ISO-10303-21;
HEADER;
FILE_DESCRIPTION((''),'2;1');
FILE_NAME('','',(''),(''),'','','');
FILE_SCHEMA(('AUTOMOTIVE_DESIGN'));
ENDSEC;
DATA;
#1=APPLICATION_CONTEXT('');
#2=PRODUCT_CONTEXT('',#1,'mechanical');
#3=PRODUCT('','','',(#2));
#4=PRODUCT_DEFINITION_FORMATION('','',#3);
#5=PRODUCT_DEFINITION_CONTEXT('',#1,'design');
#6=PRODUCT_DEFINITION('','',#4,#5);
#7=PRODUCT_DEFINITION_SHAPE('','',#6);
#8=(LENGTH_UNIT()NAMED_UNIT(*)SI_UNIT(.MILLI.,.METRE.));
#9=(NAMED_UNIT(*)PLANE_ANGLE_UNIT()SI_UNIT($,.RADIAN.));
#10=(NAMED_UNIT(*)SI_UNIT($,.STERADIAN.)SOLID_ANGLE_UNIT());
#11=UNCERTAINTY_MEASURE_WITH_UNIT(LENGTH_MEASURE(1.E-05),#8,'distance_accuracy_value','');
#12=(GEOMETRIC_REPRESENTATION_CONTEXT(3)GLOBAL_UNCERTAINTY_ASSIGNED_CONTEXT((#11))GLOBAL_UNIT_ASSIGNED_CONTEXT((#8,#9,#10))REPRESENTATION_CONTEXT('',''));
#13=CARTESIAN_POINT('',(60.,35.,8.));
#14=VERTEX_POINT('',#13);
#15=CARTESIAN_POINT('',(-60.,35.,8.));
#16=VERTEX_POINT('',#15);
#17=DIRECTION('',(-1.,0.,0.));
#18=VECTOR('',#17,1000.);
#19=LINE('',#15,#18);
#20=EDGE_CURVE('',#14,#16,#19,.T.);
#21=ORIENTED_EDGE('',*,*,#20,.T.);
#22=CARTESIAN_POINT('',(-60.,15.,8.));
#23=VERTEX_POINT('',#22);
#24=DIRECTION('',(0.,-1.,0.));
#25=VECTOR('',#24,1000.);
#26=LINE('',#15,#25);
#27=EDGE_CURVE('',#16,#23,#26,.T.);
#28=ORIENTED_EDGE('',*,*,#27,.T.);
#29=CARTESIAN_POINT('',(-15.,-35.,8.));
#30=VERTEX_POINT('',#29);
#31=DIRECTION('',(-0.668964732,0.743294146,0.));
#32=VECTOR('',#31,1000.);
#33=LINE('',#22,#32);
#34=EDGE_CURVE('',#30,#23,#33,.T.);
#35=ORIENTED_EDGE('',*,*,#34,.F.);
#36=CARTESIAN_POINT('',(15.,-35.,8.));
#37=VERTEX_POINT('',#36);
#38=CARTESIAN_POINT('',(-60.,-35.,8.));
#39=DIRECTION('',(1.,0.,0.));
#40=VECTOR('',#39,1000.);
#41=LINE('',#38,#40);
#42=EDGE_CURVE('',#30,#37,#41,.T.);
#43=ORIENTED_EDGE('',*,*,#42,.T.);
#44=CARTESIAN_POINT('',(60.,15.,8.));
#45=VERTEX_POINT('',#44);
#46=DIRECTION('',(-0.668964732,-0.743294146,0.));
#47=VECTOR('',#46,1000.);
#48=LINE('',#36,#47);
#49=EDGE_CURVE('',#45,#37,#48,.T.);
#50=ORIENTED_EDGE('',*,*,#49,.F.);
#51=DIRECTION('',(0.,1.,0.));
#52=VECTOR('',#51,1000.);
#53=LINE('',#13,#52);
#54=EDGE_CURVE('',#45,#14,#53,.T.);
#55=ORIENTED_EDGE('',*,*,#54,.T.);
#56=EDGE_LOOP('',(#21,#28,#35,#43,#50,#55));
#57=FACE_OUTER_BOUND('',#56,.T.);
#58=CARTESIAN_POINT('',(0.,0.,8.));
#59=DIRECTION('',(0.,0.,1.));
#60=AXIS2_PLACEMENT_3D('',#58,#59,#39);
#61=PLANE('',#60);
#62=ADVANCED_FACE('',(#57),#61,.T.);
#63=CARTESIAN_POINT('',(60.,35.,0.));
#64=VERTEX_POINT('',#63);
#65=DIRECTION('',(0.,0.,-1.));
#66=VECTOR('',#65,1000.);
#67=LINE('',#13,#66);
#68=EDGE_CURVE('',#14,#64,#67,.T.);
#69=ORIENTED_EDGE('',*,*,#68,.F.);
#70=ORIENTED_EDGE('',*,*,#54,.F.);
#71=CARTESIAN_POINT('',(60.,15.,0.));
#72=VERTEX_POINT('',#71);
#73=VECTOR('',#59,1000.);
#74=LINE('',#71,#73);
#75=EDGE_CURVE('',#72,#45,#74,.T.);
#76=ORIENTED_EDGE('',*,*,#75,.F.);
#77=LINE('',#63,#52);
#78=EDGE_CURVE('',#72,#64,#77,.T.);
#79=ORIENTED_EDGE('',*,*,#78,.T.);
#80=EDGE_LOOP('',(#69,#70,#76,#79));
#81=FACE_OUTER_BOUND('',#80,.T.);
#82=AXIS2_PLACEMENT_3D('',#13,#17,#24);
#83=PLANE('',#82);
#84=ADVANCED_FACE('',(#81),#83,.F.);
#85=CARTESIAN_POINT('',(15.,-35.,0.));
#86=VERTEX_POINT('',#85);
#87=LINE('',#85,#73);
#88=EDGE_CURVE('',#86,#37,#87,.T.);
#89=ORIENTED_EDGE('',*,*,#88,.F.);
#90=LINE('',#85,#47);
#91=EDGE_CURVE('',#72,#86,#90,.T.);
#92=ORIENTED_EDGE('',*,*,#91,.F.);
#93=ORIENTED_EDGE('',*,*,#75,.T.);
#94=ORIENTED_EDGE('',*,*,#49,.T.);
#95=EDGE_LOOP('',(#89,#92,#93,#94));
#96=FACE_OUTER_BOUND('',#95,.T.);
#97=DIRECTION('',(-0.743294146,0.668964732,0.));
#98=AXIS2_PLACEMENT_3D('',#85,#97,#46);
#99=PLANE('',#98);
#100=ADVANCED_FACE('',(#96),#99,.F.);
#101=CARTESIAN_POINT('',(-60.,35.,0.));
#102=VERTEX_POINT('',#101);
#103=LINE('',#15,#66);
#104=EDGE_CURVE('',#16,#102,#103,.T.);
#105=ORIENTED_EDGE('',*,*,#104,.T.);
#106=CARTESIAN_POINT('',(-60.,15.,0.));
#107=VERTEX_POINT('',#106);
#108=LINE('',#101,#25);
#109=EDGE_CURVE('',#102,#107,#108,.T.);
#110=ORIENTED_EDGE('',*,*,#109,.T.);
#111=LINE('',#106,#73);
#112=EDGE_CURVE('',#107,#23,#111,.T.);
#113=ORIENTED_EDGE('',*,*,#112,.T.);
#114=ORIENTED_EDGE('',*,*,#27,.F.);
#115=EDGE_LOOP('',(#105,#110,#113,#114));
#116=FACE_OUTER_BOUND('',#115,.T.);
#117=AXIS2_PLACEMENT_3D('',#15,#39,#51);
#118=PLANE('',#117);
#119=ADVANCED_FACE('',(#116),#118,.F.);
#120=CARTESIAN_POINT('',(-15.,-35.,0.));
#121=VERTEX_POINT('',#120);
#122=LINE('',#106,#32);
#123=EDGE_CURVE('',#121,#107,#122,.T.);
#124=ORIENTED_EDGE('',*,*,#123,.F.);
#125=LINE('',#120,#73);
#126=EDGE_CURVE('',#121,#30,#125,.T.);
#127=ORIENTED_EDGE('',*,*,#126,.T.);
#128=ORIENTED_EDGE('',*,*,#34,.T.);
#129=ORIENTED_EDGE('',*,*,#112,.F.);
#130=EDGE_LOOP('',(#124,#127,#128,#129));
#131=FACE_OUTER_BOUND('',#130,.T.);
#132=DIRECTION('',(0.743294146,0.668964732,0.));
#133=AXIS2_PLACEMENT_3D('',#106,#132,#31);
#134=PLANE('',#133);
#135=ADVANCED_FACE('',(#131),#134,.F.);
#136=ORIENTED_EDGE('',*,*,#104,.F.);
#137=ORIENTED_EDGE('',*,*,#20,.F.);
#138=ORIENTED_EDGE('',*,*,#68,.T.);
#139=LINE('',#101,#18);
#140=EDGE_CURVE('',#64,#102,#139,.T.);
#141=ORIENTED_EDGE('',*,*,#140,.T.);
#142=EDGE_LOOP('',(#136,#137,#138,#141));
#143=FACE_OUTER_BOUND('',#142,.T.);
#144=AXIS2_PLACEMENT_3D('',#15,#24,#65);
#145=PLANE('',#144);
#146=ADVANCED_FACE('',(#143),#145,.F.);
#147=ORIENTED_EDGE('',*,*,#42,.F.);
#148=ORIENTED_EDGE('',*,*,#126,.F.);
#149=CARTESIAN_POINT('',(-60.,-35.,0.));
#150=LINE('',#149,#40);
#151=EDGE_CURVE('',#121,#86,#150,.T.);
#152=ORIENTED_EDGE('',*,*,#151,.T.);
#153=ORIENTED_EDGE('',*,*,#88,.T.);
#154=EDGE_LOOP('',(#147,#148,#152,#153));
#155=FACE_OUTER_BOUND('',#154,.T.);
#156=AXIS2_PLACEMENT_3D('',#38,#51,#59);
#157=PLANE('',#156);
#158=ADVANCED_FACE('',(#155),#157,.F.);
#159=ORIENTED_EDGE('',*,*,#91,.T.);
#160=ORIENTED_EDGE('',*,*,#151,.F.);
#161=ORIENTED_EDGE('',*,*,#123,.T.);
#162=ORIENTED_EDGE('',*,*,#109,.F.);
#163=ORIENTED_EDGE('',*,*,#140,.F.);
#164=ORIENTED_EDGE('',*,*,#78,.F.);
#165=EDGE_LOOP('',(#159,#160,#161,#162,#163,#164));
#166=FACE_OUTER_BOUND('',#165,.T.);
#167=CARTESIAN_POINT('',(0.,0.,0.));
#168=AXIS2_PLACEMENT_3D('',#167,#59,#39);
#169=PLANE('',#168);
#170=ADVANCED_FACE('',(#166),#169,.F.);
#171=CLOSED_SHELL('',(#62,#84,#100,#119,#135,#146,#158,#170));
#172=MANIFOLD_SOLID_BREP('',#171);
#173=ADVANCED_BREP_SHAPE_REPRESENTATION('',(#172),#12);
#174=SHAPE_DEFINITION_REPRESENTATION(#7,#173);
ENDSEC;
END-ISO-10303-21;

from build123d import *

# Parameters (mm, degrees)
SKETCH1_W           = 120
SKETCH1_H           = 70
BOSS_EXTRUDE1_DEPTH = 8
CUT_EXTRUDE1_DEPTH  = 8


with BuildPart() as part:
    # Sketch1 → Boss-Extrude1 (new body)
    with BuildSketch(Plane.XY):
        Rectangle(SKETCH1_W, SKETCH1_H)
    extrude(amount=BOSS_EXTRUDE1_DEPTH)

    # Sketch2 → Cut-Extrude1 (cut)
    with BuildSketch(Plane.XY.offset(8)):
        Polygon((-60, 15), (-15, -35), (-60, -35), align=None)
        Polygon((15, -35), (60, 15), (60, -35), align=None)
    extrude(amount=-CUT_EXTRUDE1_DEPTH, mode=Mode.SUBTRACT)


solid = part.part
